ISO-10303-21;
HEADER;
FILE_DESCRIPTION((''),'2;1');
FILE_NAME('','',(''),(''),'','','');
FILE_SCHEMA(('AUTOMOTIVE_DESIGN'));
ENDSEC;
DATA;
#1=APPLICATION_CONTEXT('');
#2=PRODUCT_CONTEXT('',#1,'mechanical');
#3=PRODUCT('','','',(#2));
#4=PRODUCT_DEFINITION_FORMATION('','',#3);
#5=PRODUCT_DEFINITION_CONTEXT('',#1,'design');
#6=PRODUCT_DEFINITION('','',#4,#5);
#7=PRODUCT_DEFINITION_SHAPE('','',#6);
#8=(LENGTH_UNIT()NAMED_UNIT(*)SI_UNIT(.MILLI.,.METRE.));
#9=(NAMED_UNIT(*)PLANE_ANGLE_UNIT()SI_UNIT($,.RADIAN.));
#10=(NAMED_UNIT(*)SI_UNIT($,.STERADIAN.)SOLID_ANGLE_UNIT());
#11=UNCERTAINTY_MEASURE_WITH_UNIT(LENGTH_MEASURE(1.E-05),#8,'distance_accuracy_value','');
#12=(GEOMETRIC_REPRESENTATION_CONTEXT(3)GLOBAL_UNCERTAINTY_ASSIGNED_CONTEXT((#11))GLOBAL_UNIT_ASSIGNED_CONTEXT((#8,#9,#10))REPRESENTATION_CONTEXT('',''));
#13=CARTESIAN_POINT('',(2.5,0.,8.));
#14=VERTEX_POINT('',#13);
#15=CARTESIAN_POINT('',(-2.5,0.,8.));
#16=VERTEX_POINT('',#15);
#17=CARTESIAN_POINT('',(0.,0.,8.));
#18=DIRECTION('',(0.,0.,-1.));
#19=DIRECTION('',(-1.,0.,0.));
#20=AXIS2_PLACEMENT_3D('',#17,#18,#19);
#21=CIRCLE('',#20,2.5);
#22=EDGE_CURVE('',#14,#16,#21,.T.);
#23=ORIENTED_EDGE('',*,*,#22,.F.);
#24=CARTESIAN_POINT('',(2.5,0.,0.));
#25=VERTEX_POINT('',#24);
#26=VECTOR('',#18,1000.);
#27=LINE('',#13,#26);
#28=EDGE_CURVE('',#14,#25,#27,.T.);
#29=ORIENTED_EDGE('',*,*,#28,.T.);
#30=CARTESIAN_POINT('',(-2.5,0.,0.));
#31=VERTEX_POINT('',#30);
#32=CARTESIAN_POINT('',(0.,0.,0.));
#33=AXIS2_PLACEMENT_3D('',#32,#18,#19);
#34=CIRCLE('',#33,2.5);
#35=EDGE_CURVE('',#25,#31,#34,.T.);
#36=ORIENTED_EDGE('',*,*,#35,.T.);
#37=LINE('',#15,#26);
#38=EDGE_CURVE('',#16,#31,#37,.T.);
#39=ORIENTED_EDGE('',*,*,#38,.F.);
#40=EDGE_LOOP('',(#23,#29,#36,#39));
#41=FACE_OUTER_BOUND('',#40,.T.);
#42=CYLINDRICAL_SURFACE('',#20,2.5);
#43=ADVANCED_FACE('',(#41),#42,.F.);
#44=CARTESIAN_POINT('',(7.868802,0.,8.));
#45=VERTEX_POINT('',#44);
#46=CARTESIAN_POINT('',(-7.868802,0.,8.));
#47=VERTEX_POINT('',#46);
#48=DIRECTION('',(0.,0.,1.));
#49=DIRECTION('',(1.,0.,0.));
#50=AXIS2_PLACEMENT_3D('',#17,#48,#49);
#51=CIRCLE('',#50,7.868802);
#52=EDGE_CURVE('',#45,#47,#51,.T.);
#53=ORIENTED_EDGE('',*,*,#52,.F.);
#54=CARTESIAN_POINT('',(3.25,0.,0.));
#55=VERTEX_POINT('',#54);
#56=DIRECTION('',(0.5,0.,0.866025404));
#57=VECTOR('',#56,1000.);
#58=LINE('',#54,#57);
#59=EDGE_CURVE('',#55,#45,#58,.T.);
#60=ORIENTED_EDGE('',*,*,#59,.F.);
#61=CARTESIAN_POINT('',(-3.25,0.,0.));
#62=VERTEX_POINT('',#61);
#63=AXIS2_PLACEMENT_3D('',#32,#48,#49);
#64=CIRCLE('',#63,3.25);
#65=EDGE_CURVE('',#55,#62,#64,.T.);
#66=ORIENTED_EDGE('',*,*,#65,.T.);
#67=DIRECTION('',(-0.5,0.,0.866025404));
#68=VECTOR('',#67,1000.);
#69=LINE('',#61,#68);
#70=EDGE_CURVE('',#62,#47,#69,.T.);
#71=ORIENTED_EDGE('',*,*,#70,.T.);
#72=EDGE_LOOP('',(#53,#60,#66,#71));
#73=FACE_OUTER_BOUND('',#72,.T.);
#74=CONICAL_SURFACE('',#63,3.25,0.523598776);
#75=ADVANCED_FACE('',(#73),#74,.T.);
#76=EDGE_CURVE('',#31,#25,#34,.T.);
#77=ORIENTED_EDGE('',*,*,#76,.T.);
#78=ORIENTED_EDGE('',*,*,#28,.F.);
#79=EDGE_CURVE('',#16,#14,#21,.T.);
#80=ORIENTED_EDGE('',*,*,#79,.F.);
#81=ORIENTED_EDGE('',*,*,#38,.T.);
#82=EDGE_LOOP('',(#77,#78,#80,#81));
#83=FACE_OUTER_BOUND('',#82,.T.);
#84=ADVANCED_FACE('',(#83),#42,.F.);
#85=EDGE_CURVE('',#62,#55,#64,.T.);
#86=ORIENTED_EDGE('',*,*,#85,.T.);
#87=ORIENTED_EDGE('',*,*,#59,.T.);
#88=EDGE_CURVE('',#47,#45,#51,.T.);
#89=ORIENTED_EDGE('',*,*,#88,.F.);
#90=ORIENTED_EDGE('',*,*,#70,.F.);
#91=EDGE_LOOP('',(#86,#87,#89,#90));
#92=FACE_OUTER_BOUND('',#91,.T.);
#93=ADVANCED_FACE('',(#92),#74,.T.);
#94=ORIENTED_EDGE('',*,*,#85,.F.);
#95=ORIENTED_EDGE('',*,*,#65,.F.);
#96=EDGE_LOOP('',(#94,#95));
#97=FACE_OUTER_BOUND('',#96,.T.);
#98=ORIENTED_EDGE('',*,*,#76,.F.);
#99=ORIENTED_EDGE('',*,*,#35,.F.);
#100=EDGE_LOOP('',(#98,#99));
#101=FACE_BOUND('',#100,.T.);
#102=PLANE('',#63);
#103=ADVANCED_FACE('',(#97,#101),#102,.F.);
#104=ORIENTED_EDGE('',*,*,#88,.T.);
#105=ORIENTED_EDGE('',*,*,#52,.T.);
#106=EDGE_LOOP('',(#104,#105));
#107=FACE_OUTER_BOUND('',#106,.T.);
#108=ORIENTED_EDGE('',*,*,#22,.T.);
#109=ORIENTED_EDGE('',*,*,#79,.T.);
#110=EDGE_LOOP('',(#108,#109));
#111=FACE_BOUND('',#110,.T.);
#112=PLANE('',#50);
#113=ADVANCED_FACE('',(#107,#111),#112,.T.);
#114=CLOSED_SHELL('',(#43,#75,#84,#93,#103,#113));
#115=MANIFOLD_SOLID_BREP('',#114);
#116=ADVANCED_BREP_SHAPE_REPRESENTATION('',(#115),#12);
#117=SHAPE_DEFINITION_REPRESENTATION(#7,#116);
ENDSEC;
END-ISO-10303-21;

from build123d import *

# Parameters (mm, degrees)
SKETCH1_R           = 3.25
BOSS_EXTRUDE1_DEPTH = 8
BOSS_EXTRUDE1_DRAFT = -30
SKETCH2_R           = 2.5
CUT_EXTRUDE1_DEPTH  = 14.705330885


with BuildPart() as part:
    # Sketch1 → Boss-Extrude1 (with draft: the straight prism first)
    with BuildSketch(Plane.XY):
        Circle(SKETCH1_R)
    extrude(amount=BOSS_EXTRUDE1_DEPTH)
    # Boss-Extrude1: the draft: its side faces are tilted about the plane it starts from
    boss_extrude1_sides = [part.faces().sort_by_distance(p)[0] for p in [
        (-3.25, 0, 4),
    ]]
    draft(boss_extrude1_sides, Plane.XY, BOSS_EXTRUDE1_DRAFT)

    # Sketch2 → Cut-Extrude1 (cut, through all)
    with BuildSketch(Plane(origin=(0, 0, 0), x_dir=(-1, 0, 0), z_dir=(0, 0, -1))):
        Circle(SKETCH2_R)
    extrude(amount=-CUT_EXTRUDE1_DEPTH, mode=Mode.SUBTRACT)


solid = part.part
